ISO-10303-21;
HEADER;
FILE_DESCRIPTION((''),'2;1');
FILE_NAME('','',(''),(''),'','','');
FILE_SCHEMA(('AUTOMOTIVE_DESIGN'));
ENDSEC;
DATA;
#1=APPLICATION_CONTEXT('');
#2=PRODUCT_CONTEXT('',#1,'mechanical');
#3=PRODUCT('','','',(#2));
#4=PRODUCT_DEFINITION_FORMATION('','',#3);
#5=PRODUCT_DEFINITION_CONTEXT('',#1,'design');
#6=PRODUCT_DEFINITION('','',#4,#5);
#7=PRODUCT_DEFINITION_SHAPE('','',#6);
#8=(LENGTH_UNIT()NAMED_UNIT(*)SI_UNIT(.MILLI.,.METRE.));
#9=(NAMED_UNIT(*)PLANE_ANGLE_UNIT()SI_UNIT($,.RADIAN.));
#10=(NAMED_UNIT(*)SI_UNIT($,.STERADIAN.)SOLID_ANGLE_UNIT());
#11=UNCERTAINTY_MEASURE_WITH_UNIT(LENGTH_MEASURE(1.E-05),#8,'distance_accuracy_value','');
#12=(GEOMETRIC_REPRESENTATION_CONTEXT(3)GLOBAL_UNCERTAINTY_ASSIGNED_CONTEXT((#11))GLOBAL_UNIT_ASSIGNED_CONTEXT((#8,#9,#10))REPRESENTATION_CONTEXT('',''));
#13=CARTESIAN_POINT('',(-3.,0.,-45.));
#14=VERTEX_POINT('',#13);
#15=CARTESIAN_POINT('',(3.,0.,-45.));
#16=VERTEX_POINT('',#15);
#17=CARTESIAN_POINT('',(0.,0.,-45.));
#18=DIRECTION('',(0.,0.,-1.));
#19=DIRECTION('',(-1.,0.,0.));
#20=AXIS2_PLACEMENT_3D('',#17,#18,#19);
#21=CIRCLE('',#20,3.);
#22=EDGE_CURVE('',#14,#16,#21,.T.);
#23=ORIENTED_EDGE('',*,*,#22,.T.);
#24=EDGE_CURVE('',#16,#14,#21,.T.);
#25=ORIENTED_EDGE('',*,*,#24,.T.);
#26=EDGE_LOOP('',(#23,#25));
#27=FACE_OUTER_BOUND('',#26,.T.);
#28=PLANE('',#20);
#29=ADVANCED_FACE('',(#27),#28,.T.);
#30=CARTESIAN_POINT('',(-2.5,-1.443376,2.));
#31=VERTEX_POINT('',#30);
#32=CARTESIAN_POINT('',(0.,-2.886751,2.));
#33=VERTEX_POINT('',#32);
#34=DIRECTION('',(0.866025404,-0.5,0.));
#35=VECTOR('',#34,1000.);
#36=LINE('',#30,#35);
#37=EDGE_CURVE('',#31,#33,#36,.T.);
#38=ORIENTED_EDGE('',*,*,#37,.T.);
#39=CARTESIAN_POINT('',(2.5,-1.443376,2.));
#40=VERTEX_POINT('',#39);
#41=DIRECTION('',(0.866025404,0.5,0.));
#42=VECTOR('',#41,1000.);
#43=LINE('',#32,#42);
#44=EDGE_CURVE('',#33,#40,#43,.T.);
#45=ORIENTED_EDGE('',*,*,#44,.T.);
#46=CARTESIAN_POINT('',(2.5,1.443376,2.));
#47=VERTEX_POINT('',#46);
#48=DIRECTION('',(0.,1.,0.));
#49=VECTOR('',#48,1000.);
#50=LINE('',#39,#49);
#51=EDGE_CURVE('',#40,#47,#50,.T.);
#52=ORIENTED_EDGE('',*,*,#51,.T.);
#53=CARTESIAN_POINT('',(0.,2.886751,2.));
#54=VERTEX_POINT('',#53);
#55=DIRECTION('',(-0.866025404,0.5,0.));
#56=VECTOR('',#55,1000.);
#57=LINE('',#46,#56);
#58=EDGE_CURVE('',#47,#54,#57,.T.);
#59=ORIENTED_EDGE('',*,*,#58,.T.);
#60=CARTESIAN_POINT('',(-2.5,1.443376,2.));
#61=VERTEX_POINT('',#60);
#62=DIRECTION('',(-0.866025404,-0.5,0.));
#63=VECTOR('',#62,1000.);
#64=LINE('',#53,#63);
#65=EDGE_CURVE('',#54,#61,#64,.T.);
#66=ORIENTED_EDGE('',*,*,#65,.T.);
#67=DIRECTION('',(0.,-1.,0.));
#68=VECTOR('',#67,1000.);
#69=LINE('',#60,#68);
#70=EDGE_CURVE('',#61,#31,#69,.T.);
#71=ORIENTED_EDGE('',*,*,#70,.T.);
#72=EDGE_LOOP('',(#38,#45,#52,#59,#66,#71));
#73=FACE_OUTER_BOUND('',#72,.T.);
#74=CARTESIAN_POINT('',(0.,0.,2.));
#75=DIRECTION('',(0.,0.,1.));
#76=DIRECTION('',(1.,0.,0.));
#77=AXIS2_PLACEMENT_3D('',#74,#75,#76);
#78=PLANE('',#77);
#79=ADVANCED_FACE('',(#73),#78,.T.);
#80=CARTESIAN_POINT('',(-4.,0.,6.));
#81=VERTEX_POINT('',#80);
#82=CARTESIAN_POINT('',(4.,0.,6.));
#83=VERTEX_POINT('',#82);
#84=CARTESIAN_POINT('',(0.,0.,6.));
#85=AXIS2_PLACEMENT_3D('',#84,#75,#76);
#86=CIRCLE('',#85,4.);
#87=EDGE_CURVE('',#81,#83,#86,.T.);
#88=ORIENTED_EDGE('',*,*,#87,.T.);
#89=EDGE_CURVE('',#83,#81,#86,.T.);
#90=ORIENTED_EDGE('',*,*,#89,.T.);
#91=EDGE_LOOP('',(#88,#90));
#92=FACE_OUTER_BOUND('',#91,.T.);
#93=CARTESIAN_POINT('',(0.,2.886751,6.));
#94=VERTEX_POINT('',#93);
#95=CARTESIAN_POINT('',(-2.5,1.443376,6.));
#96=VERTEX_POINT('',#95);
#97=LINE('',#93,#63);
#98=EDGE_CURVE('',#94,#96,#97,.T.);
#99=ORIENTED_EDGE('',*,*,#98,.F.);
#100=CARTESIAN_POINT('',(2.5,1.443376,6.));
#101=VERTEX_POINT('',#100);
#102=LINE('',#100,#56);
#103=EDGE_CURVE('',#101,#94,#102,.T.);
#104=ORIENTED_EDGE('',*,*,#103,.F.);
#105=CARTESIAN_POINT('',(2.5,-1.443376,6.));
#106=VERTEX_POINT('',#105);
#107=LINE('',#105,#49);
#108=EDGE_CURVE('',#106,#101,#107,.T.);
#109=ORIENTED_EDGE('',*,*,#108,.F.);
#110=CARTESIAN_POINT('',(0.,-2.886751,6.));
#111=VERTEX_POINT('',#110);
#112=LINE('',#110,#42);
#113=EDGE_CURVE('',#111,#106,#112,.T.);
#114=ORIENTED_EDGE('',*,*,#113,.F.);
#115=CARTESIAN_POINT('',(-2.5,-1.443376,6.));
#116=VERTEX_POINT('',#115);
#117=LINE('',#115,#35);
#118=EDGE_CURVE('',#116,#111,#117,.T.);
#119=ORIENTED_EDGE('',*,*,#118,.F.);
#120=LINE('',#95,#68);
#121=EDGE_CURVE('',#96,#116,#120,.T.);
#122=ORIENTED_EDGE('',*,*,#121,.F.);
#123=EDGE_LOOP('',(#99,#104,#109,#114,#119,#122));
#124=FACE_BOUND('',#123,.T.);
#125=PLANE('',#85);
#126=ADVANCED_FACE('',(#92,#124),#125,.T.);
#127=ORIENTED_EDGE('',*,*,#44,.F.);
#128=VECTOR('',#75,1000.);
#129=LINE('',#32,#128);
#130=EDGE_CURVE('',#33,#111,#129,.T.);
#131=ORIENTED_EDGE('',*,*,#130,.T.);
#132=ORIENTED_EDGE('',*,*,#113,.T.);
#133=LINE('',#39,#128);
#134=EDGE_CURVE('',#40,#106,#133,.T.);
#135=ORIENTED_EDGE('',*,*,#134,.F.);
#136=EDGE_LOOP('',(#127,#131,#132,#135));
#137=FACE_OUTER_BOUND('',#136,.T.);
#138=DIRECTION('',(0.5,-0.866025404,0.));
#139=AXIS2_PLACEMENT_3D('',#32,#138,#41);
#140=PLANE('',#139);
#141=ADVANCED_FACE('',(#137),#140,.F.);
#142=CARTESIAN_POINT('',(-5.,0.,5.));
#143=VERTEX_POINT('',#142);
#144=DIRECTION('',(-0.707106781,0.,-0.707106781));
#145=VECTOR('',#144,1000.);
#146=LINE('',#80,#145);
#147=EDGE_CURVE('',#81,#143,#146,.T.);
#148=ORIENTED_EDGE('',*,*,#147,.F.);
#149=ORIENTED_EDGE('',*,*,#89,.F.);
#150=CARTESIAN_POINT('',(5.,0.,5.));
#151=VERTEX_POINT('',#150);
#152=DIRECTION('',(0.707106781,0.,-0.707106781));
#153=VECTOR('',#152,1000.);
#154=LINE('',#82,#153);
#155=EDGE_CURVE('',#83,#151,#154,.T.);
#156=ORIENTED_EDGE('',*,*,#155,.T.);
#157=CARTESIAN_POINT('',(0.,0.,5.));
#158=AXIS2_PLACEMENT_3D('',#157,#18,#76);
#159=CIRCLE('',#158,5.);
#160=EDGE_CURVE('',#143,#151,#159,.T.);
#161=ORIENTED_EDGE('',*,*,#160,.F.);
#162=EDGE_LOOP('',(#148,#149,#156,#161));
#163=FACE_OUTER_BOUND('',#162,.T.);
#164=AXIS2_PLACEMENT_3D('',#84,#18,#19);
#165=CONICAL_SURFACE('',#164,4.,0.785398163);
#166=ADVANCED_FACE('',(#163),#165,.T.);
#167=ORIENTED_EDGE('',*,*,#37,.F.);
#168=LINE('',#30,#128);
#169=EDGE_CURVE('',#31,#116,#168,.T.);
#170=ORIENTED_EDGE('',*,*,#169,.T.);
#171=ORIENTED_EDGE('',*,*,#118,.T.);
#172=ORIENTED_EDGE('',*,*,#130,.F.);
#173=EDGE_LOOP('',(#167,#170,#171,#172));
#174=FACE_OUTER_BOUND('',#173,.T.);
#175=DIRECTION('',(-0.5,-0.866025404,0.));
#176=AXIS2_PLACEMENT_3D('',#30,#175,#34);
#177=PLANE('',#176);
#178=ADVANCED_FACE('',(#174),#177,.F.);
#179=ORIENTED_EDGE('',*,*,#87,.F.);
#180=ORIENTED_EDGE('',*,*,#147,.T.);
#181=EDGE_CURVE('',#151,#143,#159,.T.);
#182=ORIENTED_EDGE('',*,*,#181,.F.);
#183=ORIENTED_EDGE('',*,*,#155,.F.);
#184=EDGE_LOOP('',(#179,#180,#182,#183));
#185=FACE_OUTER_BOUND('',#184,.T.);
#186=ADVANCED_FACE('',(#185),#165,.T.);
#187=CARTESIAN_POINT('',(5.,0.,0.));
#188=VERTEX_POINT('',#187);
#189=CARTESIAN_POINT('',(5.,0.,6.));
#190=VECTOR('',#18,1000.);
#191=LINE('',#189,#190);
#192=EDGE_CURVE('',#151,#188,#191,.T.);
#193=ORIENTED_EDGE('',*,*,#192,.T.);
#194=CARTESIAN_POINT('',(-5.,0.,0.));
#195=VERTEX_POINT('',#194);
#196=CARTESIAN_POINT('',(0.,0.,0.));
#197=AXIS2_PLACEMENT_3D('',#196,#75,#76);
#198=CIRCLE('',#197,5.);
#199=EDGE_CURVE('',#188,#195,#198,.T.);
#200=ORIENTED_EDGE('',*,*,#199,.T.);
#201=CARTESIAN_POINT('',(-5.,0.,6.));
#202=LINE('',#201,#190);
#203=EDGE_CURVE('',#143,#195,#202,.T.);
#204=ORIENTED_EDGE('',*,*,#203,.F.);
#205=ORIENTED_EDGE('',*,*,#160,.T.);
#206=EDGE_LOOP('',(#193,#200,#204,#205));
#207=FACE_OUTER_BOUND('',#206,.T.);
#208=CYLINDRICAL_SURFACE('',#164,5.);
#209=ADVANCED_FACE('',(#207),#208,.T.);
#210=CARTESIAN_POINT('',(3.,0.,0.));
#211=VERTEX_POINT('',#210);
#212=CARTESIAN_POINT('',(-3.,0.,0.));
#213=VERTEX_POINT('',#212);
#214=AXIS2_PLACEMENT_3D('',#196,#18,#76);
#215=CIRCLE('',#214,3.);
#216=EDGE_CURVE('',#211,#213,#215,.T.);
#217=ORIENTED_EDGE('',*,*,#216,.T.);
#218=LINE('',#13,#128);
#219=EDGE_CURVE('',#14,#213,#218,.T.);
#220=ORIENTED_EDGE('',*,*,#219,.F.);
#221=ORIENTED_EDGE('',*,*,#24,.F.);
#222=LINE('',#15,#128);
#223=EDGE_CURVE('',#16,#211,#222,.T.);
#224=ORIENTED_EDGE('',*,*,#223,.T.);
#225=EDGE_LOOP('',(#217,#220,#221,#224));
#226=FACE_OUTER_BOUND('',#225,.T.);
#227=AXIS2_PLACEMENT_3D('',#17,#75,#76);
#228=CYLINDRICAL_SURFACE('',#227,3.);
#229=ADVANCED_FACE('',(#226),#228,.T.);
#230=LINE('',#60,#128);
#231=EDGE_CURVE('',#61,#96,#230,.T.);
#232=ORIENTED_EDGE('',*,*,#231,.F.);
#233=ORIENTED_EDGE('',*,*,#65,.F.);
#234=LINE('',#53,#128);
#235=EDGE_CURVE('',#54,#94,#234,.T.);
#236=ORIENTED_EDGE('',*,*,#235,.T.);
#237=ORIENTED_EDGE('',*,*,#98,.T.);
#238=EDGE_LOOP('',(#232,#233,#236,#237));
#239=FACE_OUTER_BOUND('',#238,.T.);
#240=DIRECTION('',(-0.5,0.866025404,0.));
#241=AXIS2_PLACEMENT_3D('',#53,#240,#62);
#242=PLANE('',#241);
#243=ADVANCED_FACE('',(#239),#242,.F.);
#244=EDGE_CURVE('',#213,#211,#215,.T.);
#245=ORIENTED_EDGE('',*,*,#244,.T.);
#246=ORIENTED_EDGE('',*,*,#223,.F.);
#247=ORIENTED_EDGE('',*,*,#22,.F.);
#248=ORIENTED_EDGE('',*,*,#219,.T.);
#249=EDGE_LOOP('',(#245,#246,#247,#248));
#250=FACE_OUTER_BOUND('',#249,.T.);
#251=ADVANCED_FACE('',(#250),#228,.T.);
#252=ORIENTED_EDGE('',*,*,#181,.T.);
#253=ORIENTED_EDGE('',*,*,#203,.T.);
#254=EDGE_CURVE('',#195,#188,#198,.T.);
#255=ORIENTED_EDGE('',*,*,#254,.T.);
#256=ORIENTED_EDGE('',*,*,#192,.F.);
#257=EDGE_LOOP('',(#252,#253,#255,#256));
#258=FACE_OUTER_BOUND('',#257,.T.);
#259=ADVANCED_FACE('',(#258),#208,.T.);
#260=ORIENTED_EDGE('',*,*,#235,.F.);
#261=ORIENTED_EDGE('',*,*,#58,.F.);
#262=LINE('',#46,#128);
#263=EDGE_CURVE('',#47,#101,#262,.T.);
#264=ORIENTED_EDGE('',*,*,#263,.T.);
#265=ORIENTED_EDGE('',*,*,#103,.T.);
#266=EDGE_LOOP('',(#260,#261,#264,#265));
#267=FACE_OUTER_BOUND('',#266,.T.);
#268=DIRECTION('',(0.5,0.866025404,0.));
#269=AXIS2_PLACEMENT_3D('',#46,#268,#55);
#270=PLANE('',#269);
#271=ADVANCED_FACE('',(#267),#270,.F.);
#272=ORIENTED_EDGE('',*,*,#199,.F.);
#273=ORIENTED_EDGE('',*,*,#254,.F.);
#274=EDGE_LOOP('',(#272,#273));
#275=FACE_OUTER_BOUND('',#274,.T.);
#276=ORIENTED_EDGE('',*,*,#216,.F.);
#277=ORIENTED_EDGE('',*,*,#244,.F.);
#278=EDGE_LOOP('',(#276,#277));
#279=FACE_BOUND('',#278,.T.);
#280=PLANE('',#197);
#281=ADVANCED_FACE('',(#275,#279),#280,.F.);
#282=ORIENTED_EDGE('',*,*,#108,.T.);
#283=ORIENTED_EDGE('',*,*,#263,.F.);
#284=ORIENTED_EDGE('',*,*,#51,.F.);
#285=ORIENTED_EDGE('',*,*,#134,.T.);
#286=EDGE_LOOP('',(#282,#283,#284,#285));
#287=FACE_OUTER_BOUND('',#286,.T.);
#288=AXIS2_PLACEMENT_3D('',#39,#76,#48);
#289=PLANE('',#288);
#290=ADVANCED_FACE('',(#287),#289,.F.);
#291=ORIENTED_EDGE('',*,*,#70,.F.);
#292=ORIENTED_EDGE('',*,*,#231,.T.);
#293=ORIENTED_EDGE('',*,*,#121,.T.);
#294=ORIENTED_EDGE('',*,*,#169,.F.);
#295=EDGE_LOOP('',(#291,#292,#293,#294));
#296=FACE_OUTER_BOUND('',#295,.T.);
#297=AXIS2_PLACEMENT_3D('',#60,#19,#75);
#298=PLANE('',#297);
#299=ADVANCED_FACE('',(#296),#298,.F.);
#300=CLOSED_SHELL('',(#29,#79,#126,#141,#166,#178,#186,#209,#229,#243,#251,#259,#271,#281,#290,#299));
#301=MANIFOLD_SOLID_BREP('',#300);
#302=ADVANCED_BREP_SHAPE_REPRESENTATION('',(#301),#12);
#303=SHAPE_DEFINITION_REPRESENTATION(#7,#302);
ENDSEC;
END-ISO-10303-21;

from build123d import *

# Parameters (mm, degrees)
SKETCH_1_R          = 5
EXTRUDE_1_DEPTH     = 6
CUT_EXTRUDE_1_DEPTH = 4
CHAMFER_1_SIZE      = 1
SKETCH_3_R          = 3
EXTRUDE_2_DEPTH     = 45


with BuildPart() as part:
    # 草图1 → 凸台-拉伸1 (new body)
    with BuildSketch(Plane.XY):
        Circle(SKETCH_1_R)
    extrude(amount=EXTRUDE_1_DEPTH)

    # 草图2 → 切除-拉伸1 (cut)
    with BuildSketch(Plane.XY.offset(6)):
        Polygon((0, 2.886751346), (-2.5, 1.443375673), (-2.5, -1.443375673), (0, -2.886751346), (2.5, -1.443375673), (2.5, 1.443375673), align=None)
    extrude(amount=-CUT_EXTRUDE_1_DEPTH, mode=Mode.SUBTRACT)

    # 倒角1
    chamfer_1_edges = [part.edges().sort_by_distance(p)[0] for p in [
        (-5, 0, 6),
    ]]
    chamfer(chamfer_1_edges, length=CHAMFER_1_SIZE)

    # 草图3 → 凸台-拉伸2 (add)
    with BuildSketch(Plane(origin=(0, 0, 0), x_dir=(-1, 0, 0), z_dir=(0, 0, -1))):
        with Locations(Location((0, 0, 0), (0, 0, 180))):
            Circle(SKETCH_3_R)
    extrude(amount=EXTRUDE_2_DEPTH)


solid = part.part
